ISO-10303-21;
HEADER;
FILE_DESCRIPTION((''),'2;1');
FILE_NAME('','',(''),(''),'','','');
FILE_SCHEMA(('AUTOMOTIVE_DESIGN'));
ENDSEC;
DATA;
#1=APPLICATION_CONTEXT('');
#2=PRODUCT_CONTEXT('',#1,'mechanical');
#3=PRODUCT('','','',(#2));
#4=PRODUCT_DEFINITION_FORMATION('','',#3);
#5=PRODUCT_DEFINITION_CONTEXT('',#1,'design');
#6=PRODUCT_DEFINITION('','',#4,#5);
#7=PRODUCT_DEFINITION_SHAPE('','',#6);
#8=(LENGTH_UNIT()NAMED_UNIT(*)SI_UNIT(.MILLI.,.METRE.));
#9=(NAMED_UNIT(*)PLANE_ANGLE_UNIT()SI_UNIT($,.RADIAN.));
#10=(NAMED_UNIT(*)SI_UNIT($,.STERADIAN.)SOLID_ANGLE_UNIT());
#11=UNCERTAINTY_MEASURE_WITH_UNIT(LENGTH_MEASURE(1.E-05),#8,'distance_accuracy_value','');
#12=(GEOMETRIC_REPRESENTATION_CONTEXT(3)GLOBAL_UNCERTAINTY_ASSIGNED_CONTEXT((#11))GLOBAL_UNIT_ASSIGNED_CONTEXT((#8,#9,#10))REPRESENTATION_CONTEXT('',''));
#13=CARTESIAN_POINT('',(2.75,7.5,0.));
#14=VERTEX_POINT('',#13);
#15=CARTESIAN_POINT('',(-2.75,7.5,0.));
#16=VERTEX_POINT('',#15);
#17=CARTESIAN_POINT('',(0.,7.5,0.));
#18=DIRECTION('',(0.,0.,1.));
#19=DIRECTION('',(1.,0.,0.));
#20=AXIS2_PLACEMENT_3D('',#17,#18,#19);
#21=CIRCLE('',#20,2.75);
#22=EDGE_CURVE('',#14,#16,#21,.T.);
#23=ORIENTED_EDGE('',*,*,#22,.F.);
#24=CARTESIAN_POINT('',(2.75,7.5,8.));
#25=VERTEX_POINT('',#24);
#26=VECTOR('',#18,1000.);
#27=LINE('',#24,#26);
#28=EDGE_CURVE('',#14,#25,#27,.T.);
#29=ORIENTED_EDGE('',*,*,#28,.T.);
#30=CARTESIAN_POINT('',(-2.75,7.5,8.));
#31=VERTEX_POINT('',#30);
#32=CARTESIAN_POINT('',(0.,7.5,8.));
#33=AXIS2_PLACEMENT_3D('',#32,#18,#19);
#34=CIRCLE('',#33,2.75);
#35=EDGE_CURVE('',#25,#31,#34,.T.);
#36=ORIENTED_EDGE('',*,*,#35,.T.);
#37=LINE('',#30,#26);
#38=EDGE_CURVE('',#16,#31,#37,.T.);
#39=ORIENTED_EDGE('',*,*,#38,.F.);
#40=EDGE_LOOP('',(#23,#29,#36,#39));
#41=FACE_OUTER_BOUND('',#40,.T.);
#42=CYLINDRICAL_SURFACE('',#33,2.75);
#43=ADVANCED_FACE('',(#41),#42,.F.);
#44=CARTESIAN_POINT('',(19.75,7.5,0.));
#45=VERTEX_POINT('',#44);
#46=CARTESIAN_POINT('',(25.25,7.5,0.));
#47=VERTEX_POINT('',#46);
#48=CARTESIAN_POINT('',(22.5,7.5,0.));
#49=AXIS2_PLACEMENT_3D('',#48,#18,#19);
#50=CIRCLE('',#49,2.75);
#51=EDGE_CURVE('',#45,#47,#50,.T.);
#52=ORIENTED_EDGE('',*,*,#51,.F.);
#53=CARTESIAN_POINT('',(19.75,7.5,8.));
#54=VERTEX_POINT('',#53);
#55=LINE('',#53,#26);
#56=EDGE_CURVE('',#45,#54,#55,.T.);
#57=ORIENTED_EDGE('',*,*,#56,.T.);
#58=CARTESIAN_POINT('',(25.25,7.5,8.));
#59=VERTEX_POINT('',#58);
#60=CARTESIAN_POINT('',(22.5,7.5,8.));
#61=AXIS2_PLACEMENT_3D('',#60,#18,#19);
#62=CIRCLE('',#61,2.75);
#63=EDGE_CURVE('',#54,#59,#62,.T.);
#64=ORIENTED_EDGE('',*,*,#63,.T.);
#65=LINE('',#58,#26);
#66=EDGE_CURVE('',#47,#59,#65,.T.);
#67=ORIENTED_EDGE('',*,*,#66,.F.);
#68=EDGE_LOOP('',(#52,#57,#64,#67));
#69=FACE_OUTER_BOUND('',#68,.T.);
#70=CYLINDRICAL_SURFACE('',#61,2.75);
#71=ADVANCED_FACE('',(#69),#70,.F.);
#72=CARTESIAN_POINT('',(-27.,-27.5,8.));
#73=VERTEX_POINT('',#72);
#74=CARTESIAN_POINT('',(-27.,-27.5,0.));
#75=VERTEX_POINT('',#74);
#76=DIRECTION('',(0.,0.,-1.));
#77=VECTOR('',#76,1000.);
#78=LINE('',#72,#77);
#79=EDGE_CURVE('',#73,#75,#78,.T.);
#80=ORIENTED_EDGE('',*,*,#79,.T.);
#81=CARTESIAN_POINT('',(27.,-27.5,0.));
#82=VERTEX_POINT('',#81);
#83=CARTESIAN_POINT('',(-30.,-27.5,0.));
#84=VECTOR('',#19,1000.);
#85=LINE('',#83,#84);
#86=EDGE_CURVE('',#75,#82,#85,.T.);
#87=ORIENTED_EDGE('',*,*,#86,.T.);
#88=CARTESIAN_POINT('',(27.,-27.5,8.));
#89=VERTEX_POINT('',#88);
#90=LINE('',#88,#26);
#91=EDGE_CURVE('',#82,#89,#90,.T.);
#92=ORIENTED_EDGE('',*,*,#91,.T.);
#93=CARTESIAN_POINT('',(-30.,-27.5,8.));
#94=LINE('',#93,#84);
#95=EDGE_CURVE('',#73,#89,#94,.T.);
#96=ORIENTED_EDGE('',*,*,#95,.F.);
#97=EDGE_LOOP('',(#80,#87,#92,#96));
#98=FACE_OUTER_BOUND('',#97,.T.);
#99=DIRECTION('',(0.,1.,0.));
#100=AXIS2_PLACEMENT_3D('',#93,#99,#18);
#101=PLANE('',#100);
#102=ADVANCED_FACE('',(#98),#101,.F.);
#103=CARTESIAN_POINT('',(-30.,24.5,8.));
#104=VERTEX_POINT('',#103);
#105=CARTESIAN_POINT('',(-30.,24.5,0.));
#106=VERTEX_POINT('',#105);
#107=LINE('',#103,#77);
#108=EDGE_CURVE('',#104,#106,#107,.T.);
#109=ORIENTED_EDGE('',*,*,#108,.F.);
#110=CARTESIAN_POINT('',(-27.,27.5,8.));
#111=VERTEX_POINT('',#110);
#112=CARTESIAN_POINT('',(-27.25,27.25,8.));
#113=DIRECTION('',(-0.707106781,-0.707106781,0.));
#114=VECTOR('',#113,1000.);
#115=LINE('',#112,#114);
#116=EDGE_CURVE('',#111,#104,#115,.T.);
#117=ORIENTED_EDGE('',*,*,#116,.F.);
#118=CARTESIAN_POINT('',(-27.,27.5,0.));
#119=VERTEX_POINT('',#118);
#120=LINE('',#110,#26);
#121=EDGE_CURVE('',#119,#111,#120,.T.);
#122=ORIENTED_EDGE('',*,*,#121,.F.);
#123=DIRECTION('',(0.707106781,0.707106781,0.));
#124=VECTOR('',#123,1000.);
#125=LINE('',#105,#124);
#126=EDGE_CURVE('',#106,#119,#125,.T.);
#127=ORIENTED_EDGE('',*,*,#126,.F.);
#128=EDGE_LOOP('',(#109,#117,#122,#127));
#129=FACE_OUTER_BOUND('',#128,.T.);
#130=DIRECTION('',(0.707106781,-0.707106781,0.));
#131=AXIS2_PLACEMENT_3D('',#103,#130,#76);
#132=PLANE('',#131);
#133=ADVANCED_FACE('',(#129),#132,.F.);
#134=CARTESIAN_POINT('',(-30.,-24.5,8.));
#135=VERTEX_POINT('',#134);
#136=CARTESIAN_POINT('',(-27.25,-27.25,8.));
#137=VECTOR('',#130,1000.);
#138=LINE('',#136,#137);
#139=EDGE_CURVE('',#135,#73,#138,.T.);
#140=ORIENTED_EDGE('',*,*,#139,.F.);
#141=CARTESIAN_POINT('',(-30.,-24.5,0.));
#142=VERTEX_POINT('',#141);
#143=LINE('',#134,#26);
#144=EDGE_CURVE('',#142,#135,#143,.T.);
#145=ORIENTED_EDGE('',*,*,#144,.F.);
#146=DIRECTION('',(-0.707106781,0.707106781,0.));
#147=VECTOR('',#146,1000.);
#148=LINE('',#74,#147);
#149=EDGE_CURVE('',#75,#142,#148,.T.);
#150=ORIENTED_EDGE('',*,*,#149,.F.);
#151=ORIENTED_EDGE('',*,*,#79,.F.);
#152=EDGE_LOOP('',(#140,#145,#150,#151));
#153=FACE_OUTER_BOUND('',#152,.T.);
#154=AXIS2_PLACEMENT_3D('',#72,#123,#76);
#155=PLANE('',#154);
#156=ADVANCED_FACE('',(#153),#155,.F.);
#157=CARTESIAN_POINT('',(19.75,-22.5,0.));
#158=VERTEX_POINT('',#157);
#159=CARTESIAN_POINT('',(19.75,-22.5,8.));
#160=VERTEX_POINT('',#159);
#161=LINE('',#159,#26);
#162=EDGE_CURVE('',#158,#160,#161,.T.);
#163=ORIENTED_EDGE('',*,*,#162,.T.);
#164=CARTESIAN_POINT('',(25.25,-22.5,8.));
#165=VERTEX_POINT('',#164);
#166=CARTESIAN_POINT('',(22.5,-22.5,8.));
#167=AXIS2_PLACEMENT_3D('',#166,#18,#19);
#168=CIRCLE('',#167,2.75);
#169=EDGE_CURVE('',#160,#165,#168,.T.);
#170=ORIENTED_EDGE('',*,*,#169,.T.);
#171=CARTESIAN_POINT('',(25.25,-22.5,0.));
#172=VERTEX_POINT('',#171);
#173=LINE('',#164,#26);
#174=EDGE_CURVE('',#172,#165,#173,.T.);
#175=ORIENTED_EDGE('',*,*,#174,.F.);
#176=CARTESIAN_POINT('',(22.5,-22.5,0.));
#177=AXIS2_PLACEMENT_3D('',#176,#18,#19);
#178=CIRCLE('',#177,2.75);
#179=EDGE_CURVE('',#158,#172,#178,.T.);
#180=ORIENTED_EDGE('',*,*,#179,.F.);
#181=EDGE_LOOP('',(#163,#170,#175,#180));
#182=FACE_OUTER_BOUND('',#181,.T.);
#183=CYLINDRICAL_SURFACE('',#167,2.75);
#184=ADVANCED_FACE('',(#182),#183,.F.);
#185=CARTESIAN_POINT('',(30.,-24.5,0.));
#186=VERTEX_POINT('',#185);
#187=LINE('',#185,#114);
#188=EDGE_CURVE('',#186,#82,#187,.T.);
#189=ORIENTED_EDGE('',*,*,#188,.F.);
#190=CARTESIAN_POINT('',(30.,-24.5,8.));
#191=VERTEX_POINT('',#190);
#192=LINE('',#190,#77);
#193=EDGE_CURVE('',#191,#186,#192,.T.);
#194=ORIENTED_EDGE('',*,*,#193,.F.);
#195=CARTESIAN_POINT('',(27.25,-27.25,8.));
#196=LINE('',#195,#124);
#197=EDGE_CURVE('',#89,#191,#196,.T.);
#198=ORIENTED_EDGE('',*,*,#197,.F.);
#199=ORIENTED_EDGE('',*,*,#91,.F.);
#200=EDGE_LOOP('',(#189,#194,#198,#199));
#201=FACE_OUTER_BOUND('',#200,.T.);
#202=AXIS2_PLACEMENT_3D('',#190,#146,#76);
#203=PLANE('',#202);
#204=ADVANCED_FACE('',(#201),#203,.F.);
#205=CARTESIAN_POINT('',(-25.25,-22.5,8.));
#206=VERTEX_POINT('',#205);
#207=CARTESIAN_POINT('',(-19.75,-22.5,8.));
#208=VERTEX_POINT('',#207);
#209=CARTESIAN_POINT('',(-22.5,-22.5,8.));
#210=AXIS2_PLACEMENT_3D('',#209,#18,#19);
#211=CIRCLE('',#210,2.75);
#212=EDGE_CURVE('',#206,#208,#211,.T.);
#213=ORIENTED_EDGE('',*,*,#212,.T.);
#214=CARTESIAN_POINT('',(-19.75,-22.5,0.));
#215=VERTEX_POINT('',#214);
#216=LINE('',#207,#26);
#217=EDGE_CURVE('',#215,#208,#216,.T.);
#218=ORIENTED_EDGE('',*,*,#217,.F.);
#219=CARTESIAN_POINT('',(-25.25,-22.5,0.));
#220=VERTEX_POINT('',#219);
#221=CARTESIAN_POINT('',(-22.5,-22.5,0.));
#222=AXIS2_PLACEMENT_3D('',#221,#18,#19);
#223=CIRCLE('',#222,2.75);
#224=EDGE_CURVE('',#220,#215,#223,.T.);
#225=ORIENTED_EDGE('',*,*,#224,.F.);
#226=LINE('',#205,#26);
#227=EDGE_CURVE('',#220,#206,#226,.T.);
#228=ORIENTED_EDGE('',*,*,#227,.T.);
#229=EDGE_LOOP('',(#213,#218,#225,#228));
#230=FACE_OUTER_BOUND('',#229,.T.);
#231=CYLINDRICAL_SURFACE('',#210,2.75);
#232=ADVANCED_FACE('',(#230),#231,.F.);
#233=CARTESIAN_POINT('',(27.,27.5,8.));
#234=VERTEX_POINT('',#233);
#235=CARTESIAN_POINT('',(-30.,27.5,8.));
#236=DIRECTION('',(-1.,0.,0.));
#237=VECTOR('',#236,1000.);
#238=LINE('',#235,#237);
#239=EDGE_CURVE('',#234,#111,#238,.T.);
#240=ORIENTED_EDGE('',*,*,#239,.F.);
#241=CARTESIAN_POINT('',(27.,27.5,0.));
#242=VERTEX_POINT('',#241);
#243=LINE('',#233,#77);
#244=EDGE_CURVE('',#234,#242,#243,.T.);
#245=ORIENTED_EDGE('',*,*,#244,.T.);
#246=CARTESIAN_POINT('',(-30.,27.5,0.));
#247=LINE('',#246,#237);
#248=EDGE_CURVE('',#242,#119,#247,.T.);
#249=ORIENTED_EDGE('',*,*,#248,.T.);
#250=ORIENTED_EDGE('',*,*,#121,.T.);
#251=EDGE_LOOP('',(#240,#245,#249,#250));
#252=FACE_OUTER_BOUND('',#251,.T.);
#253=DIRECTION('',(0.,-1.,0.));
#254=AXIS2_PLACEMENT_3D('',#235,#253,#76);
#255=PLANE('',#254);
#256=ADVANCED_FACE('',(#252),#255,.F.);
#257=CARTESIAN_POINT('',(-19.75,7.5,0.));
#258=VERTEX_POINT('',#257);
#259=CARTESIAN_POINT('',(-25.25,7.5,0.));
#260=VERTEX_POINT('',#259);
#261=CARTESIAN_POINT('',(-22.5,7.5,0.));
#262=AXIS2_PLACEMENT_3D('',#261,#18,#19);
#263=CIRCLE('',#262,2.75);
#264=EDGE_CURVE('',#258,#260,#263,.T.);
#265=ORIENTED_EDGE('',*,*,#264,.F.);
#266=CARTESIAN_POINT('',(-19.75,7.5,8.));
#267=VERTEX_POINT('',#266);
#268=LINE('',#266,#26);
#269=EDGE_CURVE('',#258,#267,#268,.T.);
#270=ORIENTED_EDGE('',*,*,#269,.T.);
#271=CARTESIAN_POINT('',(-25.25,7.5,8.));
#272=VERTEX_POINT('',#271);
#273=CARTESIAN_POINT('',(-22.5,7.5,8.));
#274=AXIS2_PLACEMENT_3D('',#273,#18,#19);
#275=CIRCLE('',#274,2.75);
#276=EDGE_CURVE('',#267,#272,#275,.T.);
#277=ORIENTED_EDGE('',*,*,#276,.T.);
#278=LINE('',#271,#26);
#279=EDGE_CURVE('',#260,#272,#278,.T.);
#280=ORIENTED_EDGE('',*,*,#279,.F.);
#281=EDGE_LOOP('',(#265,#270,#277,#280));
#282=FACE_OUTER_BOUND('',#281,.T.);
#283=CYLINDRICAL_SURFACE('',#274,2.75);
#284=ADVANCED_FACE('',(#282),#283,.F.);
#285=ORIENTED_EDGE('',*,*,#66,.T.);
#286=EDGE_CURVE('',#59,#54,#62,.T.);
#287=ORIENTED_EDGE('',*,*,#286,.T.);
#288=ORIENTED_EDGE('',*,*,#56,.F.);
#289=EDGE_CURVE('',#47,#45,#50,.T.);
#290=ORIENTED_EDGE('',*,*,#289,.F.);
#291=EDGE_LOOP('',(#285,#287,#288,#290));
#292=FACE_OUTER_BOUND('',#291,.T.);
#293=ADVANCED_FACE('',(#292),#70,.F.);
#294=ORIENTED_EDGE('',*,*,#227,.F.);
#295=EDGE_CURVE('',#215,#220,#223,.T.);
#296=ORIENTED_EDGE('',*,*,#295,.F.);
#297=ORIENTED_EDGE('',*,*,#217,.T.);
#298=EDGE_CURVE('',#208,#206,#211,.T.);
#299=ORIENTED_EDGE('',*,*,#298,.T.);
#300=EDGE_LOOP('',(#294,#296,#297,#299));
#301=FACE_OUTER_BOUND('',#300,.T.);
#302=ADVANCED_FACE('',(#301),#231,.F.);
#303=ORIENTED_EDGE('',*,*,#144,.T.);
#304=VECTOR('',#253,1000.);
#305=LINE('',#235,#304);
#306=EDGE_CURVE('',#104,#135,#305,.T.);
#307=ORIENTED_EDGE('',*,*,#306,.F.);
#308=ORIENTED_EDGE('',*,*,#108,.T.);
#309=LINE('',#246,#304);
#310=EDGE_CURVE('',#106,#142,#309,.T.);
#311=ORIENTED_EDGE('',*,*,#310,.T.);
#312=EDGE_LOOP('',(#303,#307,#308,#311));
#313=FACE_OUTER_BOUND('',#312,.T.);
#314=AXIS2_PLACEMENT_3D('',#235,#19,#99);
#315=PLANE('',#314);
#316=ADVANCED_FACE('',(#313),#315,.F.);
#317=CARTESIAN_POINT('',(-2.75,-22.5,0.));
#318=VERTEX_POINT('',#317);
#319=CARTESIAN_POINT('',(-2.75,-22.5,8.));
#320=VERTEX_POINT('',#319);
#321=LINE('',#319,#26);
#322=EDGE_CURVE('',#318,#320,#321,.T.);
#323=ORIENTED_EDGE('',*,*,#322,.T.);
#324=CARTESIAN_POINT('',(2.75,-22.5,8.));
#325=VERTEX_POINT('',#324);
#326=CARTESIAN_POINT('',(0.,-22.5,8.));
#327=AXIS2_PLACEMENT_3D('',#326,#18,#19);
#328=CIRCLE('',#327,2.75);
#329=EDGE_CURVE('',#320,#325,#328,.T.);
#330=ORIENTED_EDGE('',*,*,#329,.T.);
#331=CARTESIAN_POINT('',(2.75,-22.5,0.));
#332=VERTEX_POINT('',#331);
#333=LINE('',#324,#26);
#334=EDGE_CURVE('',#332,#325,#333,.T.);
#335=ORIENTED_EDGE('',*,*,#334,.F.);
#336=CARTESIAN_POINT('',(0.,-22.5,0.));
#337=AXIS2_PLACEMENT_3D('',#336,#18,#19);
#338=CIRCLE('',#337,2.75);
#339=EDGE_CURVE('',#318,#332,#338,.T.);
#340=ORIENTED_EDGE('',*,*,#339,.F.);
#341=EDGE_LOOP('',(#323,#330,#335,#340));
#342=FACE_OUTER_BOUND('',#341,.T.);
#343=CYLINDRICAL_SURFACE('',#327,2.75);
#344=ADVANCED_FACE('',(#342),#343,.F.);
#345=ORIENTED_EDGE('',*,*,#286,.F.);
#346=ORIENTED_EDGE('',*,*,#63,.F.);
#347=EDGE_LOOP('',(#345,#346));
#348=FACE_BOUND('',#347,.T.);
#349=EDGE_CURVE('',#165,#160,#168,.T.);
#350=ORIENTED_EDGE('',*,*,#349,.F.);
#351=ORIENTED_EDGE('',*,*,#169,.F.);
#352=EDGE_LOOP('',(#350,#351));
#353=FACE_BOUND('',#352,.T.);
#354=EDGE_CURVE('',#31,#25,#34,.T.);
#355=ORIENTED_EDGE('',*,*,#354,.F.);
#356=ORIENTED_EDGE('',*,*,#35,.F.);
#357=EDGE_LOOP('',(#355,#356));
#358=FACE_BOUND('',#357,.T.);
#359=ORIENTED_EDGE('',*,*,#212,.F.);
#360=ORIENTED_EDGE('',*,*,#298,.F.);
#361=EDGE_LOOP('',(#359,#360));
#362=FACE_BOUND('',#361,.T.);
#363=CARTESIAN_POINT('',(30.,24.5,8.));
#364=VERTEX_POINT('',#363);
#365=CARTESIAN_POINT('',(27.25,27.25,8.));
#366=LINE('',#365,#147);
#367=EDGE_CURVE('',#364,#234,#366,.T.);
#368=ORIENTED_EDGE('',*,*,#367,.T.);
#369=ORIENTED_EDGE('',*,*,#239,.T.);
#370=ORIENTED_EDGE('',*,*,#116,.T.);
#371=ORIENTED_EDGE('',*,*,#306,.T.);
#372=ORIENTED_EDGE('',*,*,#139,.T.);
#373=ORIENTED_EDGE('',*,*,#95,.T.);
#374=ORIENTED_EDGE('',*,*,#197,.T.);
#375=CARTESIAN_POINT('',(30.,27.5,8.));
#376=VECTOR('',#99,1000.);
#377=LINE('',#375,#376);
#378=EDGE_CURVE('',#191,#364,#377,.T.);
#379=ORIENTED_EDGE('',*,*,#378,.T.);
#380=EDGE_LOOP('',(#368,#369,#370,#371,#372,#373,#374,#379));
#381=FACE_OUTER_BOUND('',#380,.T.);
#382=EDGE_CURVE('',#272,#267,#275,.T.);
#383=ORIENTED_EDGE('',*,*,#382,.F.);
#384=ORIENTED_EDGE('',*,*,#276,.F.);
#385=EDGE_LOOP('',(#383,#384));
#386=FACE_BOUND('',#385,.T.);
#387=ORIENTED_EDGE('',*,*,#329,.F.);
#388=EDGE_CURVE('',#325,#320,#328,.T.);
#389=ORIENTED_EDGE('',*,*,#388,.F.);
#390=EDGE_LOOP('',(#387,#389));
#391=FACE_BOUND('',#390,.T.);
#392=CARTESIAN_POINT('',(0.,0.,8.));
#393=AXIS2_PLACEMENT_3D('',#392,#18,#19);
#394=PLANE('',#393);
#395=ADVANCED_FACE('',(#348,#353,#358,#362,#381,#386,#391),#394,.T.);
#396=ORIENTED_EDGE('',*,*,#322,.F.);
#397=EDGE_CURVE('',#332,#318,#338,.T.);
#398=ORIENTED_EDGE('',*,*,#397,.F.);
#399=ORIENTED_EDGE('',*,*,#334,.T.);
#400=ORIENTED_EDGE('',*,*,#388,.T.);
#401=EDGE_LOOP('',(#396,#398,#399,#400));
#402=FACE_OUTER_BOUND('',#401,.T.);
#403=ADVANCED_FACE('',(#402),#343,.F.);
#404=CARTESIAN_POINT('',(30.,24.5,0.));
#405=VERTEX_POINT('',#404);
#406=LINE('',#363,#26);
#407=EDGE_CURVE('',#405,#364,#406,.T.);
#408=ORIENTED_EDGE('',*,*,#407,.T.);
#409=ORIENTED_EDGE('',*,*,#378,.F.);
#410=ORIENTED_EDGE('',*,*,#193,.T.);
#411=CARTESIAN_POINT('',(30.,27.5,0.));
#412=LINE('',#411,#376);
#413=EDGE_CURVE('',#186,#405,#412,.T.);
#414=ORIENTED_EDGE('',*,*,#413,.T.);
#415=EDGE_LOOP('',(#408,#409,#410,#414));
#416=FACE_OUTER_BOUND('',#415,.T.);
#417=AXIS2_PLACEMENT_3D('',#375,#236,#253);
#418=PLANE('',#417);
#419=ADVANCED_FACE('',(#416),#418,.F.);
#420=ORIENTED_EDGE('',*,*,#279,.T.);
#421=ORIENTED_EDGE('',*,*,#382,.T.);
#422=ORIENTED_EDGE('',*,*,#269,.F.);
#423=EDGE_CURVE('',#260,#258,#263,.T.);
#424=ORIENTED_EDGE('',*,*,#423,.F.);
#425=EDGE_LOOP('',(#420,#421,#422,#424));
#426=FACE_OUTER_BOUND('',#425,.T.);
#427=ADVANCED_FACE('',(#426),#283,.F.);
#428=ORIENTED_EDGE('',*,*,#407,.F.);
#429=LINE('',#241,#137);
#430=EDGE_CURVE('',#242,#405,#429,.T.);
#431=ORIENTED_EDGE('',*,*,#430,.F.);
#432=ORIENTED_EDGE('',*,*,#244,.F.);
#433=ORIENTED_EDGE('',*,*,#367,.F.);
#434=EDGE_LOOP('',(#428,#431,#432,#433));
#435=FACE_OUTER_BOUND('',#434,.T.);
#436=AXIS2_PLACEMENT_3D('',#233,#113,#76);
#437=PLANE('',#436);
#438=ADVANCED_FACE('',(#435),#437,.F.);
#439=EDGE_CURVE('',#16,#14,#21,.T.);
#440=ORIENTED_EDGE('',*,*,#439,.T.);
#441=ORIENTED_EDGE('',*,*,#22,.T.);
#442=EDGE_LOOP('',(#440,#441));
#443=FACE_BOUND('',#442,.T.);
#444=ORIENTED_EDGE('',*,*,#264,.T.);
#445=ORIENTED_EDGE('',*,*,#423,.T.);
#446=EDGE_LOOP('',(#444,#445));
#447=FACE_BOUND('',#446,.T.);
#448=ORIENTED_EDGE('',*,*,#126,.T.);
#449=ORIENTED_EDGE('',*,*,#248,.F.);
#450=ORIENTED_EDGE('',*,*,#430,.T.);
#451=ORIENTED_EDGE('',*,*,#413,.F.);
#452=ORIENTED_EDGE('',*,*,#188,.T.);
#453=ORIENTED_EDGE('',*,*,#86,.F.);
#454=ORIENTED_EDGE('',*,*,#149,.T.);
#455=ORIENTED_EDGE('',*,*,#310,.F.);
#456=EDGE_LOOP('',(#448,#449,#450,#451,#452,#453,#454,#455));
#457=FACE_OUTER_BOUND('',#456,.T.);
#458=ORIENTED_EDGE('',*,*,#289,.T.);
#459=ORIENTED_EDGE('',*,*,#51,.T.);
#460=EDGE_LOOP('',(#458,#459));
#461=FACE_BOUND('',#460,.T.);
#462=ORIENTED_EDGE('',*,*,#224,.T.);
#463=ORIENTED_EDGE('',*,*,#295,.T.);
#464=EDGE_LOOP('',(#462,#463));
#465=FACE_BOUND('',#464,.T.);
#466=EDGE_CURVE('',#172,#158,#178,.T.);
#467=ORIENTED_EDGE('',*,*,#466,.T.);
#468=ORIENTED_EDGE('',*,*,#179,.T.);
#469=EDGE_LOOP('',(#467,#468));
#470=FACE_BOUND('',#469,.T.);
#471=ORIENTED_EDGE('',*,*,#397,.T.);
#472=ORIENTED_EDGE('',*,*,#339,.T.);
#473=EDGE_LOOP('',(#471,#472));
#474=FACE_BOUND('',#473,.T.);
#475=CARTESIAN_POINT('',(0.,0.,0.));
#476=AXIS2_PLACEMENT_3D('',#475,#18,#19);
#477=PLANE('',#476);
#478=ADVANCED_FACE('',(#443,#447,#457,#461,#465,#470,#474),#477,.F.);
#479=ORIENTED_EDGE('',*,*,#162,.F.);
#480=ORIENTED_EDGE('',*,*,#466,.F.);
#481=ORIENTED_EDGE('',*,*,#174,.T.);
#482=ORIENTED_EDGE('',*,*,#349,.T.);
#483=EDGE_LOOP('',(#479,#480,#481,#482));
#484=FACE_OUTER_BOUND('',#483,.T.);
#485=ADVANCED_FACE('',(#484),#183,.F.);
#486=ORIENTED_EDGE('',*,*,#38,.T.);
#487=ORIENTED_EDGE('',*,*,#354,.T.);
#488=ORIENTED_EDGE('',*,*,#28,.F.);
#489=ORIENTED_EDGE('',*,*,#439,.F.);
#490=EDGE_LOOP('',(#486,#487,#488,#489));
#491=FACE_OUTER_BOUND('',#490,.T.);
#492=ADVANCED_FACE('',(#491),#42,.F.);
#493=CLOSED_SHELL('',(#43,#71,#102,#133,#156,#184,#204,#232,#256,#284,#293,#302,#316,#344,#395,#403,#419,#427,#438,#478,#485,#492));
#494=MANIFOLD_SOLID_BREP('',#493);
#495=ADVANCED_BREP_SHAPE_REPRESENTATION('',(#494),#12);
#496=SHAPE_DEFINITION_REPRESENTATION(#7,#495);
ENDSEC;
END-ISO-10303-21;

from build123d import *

# Parameters (mm, degrees)
SKETCH1_W                  = 60
SKETCH1_H                  = 55
BOSS_EXTRUDE1_DEPTH        = 8
F_5_5_5_5_DIAMETER_HOLE1_D = 5.5
CHAMFER1_SIZE              = 3


with BuildPart() as part:
    # Sketch1 → Boss-Extrude1 (new body)
    with BuildSketch(Plane.XY):
        Rectangle(SKETCH1_W, SKETCH1_H)
    extrude(amount=BOSS_EXTRUDE1_DEPTH)

    # Ø5.5 (5.5) Diameter Hole1 (through all)
    with Locations(Plane.XY.offset(8)):
        with Locations((-22.5, -22.5), (-22.5, 7.5), (0, 7.5), (0, -22.5), (22.5, -22.5), (22.5, 7.5)):
            Hole(F_5_5_5_5_DIAMETER_HOLE1_D / 2)

    # Chamfer1
    chamfer1_edges = [part.edges().sort_by_distance(p)[0] for p in [
        (30, -27.5, 4),
        (-30, -27.5, 4),
        (-30, 27.5, 4),
        (30, 27.5, 4),
    ]]
    chamfer(chamfer1_edges, length=CHAMFER1_SIZE)


solid = part.part
